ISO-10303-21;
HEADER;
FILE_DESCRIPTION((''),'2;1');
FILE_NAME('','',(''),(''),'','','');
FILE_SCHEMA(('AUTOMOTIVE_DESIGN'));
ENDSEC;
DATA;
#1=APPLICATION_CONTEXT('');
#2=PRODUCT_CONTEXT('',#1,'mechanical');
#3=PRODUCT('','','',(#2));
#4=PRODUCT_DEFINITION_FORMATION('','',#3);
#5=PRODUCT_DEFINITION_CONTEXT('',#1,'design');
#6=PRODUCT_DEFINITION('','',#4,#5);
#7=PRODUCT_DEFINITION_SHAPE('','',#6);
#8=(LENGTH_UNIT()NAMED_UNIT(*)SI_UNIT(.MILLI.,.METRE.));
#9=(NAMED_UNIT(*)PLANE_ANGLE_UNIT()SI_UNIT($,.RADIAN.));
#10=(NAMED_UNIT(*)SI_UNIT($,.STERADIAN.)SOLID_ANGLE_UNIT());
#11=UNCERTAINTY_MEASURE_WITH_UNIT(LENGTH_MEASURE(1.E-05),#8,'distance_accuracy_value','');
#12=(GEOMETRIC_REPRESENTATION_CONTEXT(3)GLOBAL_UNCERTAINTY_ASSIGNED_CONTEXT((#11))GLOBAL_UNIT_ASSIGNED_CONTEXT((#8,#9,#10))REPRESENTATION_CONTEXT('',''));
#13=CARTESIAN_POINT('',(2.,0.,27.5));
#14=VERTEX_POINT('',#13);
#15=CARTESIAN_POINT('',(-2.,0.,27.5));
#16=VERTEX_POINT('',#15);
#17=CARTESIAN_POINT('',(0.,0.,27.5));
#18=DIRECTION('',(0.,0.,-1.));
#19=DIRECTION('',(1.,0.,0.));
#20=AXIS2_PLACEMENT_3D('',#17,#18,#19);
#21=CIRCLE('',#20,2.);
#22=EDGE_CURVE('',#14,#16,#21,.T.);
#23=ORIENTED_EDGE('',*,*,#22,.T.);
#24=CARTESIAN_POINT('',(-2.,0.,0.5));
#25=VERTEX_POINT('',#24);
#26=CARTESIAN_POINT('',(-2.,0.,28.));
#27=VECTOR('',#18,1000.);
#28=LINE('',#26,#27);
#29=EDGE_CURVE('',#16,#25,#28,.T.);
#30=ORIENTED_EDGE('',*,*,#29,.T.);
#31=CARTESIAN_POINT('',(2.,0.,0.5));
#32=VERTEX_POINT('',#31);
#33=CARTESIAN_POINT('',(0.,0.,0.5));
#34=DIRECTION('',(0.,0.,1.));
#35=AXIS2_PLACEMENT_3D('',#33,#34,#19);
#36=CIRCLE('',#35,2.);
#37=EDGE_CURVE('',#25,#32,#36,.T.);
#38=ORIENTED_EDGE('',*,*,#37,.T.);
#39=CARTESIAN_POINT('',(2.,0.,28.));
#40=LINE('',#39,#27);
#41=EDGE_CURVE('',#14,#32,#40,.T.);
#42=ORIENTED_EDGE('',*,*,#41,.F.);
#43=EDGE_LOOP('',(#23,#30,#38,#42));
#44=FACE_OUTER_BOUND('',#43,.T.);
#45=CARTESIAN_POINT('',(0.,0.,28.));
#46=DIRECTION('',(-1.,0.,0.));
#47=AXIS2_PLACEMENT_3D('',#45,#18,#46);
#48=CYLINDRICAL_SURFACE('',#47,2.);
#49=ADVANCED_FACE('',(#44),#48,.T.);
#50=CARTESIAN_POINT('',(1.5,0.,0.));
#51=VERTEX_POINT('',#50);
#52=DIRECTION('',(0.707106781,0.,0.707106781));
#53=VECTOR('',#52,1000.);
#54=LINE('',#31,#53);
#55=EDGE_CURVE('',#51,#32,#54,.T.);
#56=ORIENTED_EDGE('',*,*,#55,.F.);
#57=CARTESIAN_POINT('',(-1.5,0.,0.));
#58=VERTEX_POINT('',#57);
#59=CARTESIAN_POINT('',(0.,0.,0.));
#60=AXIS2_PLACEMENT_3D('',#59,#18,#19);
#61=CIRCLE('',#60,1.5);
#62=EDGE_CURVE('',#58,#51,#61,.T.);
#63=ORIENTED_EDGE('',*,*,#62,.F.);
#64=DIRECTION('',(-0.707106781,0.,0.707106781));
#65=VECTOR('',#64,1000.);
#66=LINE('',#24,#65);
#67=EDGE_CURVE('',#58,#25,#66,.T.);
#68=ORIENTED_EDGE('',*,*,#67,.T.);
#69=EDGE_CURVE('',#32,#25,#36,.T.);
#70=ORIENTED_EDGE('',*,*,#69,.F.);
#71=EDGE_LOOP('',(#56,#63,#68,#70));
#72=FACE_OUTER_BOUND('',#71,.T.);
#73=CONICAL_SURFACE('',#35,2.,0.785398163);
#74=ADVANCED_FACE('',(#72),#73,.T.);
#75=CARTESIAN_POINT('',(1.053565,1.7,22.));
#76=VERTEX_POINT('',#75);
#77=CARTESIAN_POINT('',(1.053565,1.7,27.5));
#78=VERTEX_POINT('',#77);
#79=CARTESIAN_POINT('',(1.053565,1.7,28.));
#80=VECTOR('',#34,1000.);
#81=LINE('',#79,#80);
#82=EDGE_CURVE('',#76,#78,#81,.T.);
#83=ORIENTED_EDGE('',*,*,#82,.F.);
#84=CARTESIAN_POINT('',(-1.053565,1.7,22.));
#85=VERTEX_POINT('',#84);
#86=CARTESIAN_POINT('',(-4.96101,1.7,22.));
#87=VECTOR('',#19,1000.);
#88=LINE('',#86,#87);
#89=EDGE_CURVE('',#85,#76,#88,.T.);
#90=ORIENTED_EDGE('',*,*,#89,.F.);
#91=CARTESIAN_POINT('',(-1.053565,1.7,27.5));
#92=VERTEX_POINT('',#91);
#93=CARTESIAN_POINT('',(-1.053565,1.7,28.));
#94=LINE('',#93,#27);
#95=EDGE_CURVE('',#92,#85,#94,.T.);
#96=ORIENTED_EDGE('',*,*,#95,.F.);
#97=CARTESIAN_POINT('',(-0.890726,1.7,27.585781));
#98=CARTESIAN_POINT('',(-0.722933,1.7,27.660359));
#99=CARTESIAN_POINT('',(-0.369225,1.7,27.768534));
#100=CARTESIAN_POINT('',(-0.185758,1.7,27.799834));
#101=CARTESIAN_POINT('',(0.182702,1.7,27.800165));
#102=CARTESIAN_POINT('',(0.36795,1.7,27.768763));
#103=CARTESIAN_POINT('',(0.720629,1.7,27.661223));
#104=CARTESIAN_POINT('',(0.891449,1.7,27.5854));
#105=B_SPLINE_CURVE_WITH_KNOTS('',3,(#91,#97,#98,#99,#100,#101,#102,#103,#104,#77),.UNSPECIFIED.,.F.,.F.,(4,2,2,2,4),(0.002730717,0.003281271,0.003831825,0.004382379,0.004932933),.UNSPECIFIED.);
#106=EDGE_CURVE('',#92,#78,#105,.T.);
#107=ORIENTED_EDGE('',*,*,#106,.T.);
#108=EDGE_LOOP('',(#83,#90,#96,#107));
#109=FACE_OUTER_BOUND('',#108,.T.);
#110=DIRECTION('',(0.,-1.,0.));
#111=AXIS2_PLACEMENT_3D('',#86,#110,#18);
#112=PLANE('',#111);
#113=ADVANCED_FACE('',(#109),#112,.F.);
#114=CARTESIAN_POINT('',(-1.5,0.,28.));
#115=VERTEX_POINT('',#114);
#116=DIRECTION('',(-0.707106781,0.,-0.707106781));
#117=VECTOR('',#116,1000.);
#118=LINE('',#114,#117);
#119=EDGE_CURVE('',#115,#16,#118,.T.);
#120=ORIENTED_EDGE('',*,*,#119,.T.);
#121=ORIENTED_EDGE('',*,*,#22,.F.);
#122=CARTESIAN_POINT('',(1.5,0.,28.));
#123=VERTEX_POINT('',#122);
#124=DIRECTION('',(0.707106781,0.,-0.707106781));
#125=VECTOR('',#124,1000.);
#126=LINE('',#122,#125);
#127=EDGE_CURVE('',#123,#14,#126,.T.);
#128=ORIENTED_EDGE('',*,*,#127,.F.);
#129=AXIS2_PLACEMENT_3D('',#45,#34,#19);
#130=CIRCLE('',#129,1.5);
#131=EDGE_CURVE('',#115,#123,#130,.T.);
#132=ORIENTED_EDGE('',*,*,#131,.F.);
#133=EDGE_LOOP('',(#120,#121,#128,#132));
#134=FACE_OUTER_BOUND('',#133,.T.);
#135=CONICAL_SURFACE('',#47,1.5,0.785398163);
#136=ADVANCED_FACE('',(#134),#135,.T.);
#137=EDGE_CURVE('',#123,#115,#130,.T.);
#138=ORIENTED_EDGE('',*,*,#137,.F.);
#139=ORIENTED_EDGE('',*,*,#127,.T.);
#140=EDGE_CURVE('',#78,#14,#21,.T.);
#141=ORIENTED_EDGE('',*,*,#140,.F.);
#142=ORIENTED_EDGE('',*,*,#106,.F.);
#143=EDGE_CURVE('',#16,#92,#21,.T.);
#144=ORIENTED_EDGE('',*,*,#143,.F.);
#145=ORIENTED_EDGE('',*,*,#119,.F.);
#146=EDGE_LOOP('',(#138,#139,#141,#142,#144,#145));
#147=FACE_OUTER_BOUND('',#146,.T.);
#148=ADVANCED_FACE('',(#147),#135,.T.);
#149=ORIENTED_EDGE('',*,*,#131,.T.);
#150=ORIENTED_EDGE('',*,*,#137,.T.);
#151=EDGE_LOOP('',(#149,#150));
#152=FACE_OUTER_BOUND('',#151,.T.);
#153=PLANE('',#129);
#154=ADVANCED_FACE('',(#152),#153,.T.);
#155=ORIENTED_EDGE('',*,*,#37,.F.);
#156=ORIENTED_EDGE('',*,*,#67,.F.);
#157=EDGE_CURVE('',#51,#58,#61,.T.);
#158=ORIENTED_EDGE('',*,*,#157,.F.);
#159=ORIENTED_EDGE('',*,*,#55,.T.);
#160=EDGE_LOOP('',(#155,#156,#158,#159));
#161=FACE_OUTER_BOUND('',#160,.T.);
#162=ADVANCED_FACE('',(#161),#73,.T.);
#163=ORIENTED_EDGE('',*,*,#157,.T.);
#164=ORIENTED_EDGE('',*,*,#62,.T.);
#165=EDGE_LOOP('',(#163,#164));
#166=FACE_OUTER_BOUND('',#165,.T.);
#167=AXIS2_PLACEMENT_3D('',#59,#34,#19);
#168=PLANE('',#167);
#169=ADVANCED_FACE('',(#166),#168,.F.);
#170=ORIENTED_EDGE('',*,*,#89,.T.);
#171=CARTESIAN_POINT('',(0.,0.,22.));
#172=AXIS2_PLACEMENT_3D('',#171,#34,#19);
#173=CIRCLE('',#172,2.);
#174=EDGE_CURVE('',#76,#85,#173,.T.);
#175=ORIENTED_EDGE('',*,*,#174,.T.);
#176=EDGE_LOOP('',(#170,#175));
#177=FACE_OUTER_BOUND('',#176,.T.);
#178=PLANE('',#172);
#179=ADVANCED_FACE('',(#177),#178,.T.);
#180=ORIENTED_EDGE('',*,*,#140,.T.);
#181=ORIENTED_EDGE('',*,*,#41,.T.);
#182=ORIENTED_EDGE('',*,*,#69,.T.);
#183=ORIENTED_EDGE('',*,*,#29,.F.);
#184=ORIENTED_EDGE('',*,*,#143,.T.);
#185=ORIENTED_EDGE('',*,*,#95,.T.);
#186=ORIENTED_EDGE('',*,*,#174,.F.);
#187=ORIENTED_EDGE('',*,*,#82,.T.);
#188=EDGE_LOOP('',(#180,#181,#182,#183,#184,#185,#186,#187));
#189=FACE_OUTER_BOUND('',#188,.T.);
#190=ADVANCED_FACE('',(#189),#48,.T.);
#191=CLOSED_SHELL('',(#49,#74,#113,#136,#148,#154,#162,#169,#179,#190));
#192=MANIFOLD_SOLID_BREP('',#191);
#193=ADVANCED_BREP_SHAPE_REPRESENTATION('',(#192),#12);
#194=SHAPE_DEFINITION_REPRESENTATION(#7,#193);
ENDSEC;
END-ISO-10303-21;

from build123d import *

# Parameters (mm, degrees)
SKETCH1_R           = 2
BOSS_EXTRUDE1_DEPTH = 28
CHAMFER1_SIZE       = 0.5
SKETCH3_W           = 9.979897522
SKETCH3_H           = 2.201799933
CUT_EXTRUDE1_DEPTH  = 6


with BuildPart() as part:
    # Sketch1 → Boss-Extrude1 (new body)
    with BuildSketch(Plane.XY):
        Circle(SKETCH1_R)
    extrude(amount=BOSS_EXTRUDE1_DEPTH)

    # Chamfer1
    chamfer1_edges = [part.edges().sort_by_distance(p)[0] for p in [
        (-2, 0, 0),
        (-2, 0, 28),
    ]]
    chamfer(chamfer1_edges, length=CHAMFER1_SIZE)

    # Sketch3 → Cut-Extrude1 (cut)
    with BuildSketch(Plane.XY.offset(28)):
        with Locations((0.02893888, 2.800899967)):
            Rectangle(SKETCH3_W, SKETCH3_H)
    extrude(amount=-CUT_EXTRUDE1_DEPTH, mode=Mode.SUBTRACT)


solid = part.part
